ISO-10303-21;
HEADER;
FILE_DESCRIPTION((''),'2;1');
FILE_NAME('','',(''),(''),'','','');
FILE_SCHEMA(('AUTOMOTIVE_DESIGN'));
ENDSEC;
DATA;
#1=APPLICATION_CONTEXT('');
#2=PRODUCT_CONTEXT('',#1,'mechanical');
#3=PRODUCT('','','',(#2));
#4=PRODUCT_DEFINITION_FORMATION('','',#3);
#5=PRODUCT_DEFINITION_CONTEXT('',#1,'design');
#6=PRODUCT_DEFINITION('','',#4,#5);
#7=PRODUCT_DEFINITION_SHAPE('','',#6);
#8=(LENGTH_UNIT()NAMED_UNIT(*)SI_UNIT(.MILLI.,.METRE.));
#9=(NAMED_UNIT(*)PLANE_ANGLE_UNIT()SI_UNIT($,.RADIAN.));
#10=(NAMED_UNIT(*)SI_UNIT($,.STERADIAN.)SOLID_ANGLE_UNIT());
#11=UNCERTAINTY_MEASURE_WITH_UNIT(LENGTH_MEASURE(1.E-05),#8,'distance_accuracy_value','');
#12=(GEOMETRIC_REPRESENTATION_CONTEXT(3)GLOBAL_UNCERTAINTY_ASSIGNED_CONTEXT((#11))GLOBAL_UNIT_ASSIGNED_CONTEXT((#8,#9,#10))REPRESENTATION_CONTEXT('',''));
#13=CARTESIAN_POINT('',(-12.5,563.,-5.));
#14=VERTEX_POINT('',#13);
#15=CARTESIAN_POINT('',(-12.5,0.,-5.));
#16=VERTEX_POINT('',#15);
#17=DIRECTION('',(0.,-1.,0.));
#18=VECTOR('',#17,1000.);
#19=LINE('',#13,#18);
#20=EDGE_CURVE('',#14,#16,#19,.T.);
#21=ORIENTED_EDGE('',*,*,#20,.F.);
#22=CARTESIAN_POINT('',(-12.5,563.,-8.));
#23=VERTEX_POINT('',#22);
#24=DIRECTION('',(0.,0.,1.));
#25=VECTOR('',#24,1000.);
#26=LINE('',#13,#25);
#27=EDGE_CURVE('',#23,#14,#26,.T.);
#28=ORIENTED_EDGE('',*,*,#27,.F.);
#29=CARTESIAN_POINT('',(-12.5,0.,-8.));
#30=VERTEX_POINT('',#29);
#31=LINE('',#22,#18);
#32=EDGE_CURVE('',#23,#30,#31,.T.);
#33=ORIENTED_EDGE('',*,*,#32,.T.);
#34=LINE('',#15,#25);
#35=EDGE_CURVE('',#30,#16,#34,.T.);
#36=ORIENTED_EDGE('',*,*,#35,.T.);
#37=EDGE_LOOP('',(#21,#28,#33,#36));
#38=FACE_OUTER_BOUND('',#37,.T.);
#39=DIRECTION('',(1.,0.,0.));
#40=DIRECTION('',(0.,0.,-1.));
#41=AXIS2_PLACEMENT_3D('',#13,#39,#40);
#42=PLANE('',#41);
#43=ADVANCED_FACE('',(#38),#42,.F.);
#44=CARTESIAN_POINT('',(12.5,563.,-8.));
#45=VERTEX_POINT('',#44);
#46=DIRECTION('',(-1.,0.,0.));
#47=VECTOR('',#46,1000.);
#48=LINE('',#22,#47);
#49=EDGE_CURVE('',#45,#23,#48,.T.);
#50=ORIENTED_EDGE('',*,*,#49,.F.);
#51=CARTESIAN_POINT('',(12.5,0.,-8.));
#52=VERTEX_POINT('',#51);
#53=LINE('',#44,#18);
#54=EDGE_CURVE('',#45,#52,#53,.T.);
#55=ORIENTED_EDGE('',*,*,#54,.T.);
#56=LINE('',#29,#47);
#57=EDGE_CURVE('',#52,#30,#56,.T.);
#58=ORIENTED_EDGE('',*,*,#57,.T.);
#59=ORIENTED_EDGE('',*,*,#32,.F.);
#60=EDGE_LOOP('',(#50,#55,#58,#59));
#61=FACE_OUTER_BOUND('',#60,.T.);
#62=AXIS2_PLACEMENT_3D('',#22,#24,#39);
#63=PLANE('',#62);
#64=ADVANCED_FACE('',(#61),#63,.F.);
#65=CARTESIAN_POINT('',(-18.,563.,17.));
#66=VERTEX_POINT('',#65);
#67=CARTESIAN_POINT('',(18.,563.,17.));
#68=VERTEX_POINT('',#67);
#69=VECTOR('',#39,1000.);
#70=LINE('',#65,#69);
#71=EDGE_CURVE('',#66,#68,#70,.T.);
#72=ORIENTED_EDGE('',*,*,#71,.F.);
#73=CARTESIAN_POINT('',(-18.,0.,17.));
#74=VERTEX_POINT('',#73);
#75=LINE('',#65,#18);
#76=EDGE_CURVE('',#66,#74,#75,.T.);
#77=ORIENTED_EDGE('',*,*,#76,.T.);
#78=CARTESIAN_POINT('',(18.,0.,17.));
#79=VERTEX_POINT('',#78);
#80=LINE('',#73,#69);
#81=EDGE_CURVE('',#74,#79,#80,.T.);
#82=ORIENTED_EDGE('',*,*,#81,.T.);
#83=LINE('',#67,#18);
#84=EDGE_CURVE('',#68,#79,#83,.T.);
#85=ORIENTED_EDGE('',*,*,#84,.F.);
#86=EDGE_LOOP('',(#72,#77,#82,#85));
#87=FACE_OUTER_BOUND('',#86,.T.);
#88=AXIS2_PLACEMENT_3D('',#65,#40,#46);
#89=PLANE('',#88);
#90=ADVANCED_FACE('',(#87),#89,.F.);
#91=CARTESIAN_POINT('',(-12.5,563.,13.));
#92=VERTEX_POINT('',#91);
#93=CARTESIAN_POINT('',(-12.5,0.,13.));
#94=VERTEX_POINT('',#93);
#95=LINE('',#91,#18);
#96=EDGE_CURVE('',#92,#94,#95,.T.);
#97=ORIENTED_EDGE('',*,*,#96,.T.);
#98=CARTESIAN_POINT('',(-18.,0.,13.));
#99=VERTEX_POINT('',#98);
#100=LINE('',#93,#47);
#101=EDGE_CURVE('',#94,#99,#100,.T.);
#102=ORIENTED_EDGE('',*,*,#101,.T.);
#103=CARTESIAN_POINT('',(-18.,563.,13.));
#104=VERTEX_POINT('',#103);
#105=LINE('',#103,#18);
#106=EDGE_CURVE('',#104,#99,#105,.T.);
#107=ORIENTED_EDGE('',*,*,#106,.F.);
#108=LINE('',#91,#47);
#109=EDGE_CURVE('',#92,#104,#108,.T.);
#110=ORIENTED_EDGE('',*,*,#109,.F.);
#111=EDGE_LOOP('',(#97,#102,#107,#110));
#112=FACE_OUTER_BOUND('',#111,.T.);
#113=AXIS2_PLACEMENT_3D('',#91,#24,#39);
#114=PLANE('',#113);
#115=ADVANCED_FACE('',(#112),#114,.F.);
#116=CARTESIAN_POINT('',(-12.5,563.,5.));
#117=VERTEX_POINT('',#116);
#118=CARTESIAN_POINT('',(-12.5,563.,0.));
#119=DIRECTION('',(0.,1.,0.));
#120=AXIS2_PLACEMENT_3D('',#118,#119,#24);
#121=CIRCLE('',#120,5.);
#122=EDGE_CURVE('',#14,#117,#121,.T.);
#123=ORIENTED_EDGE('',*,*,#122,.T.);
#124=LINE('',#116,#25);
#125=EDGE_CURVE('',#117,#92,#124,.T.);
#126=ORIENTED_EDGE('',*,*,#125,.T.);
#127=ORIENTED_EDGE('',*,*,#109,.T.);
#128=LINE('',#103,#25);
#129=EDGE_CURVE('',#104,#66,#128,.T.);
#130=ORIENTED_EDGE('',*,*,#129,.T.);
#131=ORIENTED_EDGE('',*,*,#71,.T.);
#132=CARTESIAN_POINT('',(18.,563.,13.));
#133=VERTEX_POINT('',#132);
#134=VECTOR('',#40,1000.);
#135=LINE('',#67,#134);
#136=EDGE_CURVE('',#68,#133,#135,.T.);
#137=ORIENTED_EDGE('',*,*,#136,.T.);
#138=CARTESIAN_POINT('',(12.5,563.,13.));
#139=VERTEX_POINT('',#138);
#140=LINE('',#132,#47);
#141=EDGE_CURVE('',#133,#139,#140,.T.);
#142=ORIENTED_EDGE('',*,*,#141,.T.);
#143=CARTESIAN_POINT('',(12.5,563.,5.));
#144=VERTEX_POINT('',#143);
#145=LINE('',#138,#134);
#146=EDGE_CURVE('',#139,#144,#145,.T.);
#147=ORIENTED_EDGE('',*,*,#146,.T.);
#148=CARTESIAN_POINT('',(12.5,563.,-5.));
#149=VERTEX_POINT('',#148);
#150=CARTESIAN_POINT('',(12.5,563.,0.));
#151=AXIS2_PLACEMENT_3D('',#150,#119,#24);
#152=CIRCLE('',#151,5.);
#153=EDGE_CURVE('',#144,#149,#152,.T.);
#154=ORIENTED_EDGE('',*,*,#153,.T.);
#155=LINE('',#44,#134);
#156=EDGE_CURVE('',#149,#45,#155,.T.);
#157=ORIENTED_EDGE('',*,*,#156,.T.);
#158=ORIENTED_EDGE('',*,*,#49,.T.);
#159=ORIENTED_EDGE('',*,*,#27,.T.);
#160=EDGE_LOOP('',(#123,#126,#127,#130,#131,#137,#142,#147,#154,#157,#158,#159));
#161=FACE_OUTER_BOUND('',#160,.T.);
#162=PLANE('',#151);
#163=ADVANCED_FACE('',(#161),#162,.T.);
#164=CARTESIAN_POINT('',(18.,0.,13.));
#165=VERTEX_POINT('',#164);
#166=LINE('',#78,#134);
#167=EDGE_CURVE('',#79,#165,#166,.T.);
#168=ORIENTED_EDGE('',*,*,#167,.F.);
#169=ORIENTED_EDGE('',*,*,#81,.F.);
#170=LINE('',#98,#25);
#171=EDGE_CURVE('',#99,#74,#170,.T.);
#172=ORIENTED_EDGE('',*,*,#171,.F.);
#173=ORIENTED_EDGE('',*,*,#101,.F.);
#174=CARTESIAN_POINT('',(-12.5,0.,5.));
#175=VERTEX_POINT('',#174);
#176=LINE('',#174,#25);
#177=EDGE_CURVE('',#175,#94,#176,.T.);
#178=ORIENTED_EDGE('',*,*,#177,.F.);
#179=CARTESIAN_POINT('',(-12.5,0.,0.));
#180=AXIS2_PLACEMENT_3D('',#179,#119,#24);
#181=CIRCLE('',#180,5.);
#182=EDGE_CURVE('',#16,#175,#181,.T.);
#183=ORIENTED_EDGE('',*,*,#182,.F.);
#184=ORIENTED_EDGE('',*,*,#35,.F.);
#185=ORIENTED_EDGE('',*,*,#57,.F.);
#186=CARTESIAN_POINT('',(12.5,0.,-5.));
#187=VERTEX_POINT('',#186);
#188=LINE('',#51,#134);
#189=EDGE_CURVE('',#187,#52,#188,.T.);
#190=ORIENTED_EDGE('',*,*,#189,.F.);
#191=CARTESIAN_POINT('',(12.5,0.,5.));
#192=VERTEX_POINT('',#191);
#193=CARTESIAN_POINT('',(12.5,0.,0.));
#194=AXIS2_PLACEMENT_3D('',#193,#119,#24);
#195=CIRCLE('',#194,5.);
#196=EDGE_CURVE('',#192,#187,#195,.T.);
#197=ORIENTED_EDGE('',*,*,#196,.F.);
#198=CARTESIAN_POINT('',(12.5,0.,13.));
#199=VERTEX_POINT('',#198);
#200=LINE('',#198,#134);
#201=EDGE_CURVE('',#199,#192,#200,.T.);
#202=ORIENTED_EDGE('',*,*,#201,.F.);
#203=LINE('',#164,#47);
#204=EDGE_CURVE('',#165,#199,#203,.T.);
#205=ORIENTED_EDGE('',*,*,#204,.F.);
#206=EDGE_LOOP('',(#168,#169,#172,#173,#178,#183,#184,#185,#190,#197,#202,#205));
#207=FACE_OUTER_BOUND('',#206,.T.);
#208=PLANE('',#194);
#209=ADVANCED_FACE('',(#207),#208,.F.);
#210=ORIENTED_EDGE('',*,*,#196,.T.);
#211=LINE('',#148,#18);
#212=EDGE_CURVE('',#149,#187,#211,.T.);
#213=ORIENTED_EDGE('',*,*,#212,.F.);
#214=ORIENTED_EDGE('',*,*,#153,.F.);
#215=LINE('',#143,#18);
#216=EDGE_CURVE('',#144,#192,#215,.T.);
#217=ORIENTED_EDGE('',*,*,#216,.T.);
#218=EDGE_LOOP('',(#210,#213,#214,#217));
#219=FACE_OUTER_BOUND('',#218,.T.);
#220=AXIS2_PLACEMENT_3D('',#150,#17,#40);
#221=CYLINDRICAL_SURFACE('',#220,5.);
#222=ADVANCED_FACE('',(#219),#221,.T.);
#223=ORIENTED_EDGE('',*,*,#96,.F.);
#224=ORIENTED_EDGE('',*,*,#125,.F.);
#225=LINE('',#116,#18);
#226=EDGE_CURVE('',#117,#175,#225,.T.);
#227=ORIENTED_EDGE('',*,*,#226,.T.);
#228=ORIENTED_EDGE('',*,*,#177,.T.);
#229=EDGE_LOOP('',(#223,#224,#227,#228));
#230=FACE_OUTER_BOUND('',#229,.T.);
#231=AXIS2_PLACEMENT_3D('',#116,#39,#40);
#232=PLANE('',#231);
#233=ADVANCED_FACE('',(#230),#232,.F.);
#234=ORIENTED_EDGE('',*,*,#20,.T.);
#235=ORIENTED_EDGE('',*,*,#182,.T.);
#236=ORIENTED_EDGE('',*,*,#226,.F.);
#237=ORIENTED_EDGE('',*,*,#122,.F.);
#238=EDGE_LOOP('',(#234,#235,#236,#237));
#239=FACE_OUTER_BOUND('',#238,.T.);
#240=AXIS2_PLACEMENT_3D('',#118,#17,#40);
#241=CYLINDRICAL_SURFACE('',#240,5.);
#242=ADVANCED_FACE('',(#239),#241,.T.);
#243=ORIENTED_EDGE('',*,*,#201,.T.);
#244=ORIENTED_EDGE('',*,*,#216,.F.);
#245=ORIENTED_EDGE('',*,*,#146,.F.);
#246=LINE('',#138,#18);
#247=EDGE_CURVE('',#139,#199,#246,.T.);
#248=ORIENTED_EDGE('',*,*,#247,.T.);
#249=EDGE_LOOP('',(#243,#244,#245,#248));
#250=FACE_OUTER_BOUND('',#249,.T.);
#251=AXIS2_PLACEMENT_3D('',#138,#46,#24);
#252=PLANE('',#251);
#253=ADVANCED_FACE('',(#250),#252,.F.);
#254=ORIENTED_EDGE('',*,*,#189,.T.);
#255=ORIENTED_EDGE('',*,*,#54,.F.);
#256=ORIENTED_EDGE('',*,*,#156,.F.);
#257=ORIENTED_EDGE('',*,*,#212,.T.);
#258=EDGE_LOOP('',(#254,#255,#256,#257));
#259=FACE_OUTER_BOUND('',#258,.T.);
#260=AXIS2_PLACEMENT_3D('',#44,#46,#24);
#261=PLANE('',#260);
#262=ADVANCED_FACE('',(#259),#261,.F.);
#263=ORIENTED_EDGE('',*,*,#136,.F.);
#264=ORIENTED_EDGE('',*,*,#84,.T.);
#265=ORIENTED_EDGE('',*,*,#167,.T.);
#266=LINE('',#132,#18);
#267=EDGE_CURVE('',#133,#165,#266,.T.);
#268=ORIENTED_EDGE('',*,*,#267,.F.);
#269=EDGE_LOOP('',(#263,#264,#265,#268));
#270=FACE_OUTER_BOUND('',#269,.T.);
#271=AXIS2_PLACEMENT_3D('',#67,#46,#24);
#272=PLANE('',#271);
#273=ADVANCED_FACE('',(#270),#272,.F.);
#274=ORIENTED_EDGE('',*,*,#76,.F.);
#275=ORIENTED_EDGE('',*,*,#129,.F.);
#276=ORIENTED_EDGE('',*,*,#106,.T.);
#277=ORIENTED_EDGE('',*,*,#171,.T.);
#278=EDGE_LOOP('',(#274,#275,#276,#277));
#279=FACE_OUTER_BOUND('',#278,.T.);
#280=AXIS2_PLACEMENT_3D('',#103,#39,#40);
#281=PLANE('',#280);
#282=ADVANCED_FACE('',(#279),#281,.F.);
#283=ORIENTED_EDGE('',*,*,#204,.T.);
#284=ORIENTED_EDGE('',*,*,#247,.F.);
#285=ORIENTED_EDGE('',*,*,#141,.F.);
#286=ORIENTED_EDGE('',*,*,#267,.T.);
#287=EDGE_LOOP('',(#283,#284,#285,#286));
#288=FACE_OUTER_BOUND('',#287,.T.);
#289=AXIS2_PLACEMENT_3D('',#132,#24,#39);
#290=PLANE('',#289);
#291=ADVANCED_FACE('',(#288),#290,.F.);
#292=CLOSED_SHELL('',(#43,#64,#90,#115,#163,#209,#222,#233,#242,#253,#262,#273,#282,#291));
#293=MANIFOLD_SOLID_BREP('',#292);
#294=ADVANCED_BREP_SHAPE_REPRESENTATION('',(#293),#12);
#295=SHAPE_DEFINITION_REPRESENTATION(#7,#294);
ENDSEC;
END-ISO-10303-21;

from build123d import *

# Parameters (mm, degrees)
EXTRUDE_1_DEPTH = 563


with BuildPart() as part:
    # 草图1 → 凸台-拉伸1 (new body)
    with BuildSketch(Plane(origin=(0, 0, 0), x_dir=(1, 0, 0), z_dir=(0, 1, 0))):
        with BuildLine():
            Line((-12.5, 5), (-12.5, 8))
            Line((-12.5, 8), (12.5, 8))
            Line((12.5, 8), (12.5, 5))
            ThreePointArc((12.5, 5), (17.5, 0), (12.5, -5))
            Line((12.5, -5), (12.5, -13))
            Line((12.5, -13), (18, -13))
            Line((18, -13), (18, -17))
            Line((18, -17), (-18, -17))
            Line((-18, -17), (-18, -13))
            Line((-18, -13), (-12.5, -13))
            Line((-12.5, -13), (-12.5, -5))
            ThreePointArc((-12.5, -5), (-17.5, 0), (-12.5, 5))
        make_face()
    extrude(amount=EXTRUDE_1_DEPTH)


solid = part.part
